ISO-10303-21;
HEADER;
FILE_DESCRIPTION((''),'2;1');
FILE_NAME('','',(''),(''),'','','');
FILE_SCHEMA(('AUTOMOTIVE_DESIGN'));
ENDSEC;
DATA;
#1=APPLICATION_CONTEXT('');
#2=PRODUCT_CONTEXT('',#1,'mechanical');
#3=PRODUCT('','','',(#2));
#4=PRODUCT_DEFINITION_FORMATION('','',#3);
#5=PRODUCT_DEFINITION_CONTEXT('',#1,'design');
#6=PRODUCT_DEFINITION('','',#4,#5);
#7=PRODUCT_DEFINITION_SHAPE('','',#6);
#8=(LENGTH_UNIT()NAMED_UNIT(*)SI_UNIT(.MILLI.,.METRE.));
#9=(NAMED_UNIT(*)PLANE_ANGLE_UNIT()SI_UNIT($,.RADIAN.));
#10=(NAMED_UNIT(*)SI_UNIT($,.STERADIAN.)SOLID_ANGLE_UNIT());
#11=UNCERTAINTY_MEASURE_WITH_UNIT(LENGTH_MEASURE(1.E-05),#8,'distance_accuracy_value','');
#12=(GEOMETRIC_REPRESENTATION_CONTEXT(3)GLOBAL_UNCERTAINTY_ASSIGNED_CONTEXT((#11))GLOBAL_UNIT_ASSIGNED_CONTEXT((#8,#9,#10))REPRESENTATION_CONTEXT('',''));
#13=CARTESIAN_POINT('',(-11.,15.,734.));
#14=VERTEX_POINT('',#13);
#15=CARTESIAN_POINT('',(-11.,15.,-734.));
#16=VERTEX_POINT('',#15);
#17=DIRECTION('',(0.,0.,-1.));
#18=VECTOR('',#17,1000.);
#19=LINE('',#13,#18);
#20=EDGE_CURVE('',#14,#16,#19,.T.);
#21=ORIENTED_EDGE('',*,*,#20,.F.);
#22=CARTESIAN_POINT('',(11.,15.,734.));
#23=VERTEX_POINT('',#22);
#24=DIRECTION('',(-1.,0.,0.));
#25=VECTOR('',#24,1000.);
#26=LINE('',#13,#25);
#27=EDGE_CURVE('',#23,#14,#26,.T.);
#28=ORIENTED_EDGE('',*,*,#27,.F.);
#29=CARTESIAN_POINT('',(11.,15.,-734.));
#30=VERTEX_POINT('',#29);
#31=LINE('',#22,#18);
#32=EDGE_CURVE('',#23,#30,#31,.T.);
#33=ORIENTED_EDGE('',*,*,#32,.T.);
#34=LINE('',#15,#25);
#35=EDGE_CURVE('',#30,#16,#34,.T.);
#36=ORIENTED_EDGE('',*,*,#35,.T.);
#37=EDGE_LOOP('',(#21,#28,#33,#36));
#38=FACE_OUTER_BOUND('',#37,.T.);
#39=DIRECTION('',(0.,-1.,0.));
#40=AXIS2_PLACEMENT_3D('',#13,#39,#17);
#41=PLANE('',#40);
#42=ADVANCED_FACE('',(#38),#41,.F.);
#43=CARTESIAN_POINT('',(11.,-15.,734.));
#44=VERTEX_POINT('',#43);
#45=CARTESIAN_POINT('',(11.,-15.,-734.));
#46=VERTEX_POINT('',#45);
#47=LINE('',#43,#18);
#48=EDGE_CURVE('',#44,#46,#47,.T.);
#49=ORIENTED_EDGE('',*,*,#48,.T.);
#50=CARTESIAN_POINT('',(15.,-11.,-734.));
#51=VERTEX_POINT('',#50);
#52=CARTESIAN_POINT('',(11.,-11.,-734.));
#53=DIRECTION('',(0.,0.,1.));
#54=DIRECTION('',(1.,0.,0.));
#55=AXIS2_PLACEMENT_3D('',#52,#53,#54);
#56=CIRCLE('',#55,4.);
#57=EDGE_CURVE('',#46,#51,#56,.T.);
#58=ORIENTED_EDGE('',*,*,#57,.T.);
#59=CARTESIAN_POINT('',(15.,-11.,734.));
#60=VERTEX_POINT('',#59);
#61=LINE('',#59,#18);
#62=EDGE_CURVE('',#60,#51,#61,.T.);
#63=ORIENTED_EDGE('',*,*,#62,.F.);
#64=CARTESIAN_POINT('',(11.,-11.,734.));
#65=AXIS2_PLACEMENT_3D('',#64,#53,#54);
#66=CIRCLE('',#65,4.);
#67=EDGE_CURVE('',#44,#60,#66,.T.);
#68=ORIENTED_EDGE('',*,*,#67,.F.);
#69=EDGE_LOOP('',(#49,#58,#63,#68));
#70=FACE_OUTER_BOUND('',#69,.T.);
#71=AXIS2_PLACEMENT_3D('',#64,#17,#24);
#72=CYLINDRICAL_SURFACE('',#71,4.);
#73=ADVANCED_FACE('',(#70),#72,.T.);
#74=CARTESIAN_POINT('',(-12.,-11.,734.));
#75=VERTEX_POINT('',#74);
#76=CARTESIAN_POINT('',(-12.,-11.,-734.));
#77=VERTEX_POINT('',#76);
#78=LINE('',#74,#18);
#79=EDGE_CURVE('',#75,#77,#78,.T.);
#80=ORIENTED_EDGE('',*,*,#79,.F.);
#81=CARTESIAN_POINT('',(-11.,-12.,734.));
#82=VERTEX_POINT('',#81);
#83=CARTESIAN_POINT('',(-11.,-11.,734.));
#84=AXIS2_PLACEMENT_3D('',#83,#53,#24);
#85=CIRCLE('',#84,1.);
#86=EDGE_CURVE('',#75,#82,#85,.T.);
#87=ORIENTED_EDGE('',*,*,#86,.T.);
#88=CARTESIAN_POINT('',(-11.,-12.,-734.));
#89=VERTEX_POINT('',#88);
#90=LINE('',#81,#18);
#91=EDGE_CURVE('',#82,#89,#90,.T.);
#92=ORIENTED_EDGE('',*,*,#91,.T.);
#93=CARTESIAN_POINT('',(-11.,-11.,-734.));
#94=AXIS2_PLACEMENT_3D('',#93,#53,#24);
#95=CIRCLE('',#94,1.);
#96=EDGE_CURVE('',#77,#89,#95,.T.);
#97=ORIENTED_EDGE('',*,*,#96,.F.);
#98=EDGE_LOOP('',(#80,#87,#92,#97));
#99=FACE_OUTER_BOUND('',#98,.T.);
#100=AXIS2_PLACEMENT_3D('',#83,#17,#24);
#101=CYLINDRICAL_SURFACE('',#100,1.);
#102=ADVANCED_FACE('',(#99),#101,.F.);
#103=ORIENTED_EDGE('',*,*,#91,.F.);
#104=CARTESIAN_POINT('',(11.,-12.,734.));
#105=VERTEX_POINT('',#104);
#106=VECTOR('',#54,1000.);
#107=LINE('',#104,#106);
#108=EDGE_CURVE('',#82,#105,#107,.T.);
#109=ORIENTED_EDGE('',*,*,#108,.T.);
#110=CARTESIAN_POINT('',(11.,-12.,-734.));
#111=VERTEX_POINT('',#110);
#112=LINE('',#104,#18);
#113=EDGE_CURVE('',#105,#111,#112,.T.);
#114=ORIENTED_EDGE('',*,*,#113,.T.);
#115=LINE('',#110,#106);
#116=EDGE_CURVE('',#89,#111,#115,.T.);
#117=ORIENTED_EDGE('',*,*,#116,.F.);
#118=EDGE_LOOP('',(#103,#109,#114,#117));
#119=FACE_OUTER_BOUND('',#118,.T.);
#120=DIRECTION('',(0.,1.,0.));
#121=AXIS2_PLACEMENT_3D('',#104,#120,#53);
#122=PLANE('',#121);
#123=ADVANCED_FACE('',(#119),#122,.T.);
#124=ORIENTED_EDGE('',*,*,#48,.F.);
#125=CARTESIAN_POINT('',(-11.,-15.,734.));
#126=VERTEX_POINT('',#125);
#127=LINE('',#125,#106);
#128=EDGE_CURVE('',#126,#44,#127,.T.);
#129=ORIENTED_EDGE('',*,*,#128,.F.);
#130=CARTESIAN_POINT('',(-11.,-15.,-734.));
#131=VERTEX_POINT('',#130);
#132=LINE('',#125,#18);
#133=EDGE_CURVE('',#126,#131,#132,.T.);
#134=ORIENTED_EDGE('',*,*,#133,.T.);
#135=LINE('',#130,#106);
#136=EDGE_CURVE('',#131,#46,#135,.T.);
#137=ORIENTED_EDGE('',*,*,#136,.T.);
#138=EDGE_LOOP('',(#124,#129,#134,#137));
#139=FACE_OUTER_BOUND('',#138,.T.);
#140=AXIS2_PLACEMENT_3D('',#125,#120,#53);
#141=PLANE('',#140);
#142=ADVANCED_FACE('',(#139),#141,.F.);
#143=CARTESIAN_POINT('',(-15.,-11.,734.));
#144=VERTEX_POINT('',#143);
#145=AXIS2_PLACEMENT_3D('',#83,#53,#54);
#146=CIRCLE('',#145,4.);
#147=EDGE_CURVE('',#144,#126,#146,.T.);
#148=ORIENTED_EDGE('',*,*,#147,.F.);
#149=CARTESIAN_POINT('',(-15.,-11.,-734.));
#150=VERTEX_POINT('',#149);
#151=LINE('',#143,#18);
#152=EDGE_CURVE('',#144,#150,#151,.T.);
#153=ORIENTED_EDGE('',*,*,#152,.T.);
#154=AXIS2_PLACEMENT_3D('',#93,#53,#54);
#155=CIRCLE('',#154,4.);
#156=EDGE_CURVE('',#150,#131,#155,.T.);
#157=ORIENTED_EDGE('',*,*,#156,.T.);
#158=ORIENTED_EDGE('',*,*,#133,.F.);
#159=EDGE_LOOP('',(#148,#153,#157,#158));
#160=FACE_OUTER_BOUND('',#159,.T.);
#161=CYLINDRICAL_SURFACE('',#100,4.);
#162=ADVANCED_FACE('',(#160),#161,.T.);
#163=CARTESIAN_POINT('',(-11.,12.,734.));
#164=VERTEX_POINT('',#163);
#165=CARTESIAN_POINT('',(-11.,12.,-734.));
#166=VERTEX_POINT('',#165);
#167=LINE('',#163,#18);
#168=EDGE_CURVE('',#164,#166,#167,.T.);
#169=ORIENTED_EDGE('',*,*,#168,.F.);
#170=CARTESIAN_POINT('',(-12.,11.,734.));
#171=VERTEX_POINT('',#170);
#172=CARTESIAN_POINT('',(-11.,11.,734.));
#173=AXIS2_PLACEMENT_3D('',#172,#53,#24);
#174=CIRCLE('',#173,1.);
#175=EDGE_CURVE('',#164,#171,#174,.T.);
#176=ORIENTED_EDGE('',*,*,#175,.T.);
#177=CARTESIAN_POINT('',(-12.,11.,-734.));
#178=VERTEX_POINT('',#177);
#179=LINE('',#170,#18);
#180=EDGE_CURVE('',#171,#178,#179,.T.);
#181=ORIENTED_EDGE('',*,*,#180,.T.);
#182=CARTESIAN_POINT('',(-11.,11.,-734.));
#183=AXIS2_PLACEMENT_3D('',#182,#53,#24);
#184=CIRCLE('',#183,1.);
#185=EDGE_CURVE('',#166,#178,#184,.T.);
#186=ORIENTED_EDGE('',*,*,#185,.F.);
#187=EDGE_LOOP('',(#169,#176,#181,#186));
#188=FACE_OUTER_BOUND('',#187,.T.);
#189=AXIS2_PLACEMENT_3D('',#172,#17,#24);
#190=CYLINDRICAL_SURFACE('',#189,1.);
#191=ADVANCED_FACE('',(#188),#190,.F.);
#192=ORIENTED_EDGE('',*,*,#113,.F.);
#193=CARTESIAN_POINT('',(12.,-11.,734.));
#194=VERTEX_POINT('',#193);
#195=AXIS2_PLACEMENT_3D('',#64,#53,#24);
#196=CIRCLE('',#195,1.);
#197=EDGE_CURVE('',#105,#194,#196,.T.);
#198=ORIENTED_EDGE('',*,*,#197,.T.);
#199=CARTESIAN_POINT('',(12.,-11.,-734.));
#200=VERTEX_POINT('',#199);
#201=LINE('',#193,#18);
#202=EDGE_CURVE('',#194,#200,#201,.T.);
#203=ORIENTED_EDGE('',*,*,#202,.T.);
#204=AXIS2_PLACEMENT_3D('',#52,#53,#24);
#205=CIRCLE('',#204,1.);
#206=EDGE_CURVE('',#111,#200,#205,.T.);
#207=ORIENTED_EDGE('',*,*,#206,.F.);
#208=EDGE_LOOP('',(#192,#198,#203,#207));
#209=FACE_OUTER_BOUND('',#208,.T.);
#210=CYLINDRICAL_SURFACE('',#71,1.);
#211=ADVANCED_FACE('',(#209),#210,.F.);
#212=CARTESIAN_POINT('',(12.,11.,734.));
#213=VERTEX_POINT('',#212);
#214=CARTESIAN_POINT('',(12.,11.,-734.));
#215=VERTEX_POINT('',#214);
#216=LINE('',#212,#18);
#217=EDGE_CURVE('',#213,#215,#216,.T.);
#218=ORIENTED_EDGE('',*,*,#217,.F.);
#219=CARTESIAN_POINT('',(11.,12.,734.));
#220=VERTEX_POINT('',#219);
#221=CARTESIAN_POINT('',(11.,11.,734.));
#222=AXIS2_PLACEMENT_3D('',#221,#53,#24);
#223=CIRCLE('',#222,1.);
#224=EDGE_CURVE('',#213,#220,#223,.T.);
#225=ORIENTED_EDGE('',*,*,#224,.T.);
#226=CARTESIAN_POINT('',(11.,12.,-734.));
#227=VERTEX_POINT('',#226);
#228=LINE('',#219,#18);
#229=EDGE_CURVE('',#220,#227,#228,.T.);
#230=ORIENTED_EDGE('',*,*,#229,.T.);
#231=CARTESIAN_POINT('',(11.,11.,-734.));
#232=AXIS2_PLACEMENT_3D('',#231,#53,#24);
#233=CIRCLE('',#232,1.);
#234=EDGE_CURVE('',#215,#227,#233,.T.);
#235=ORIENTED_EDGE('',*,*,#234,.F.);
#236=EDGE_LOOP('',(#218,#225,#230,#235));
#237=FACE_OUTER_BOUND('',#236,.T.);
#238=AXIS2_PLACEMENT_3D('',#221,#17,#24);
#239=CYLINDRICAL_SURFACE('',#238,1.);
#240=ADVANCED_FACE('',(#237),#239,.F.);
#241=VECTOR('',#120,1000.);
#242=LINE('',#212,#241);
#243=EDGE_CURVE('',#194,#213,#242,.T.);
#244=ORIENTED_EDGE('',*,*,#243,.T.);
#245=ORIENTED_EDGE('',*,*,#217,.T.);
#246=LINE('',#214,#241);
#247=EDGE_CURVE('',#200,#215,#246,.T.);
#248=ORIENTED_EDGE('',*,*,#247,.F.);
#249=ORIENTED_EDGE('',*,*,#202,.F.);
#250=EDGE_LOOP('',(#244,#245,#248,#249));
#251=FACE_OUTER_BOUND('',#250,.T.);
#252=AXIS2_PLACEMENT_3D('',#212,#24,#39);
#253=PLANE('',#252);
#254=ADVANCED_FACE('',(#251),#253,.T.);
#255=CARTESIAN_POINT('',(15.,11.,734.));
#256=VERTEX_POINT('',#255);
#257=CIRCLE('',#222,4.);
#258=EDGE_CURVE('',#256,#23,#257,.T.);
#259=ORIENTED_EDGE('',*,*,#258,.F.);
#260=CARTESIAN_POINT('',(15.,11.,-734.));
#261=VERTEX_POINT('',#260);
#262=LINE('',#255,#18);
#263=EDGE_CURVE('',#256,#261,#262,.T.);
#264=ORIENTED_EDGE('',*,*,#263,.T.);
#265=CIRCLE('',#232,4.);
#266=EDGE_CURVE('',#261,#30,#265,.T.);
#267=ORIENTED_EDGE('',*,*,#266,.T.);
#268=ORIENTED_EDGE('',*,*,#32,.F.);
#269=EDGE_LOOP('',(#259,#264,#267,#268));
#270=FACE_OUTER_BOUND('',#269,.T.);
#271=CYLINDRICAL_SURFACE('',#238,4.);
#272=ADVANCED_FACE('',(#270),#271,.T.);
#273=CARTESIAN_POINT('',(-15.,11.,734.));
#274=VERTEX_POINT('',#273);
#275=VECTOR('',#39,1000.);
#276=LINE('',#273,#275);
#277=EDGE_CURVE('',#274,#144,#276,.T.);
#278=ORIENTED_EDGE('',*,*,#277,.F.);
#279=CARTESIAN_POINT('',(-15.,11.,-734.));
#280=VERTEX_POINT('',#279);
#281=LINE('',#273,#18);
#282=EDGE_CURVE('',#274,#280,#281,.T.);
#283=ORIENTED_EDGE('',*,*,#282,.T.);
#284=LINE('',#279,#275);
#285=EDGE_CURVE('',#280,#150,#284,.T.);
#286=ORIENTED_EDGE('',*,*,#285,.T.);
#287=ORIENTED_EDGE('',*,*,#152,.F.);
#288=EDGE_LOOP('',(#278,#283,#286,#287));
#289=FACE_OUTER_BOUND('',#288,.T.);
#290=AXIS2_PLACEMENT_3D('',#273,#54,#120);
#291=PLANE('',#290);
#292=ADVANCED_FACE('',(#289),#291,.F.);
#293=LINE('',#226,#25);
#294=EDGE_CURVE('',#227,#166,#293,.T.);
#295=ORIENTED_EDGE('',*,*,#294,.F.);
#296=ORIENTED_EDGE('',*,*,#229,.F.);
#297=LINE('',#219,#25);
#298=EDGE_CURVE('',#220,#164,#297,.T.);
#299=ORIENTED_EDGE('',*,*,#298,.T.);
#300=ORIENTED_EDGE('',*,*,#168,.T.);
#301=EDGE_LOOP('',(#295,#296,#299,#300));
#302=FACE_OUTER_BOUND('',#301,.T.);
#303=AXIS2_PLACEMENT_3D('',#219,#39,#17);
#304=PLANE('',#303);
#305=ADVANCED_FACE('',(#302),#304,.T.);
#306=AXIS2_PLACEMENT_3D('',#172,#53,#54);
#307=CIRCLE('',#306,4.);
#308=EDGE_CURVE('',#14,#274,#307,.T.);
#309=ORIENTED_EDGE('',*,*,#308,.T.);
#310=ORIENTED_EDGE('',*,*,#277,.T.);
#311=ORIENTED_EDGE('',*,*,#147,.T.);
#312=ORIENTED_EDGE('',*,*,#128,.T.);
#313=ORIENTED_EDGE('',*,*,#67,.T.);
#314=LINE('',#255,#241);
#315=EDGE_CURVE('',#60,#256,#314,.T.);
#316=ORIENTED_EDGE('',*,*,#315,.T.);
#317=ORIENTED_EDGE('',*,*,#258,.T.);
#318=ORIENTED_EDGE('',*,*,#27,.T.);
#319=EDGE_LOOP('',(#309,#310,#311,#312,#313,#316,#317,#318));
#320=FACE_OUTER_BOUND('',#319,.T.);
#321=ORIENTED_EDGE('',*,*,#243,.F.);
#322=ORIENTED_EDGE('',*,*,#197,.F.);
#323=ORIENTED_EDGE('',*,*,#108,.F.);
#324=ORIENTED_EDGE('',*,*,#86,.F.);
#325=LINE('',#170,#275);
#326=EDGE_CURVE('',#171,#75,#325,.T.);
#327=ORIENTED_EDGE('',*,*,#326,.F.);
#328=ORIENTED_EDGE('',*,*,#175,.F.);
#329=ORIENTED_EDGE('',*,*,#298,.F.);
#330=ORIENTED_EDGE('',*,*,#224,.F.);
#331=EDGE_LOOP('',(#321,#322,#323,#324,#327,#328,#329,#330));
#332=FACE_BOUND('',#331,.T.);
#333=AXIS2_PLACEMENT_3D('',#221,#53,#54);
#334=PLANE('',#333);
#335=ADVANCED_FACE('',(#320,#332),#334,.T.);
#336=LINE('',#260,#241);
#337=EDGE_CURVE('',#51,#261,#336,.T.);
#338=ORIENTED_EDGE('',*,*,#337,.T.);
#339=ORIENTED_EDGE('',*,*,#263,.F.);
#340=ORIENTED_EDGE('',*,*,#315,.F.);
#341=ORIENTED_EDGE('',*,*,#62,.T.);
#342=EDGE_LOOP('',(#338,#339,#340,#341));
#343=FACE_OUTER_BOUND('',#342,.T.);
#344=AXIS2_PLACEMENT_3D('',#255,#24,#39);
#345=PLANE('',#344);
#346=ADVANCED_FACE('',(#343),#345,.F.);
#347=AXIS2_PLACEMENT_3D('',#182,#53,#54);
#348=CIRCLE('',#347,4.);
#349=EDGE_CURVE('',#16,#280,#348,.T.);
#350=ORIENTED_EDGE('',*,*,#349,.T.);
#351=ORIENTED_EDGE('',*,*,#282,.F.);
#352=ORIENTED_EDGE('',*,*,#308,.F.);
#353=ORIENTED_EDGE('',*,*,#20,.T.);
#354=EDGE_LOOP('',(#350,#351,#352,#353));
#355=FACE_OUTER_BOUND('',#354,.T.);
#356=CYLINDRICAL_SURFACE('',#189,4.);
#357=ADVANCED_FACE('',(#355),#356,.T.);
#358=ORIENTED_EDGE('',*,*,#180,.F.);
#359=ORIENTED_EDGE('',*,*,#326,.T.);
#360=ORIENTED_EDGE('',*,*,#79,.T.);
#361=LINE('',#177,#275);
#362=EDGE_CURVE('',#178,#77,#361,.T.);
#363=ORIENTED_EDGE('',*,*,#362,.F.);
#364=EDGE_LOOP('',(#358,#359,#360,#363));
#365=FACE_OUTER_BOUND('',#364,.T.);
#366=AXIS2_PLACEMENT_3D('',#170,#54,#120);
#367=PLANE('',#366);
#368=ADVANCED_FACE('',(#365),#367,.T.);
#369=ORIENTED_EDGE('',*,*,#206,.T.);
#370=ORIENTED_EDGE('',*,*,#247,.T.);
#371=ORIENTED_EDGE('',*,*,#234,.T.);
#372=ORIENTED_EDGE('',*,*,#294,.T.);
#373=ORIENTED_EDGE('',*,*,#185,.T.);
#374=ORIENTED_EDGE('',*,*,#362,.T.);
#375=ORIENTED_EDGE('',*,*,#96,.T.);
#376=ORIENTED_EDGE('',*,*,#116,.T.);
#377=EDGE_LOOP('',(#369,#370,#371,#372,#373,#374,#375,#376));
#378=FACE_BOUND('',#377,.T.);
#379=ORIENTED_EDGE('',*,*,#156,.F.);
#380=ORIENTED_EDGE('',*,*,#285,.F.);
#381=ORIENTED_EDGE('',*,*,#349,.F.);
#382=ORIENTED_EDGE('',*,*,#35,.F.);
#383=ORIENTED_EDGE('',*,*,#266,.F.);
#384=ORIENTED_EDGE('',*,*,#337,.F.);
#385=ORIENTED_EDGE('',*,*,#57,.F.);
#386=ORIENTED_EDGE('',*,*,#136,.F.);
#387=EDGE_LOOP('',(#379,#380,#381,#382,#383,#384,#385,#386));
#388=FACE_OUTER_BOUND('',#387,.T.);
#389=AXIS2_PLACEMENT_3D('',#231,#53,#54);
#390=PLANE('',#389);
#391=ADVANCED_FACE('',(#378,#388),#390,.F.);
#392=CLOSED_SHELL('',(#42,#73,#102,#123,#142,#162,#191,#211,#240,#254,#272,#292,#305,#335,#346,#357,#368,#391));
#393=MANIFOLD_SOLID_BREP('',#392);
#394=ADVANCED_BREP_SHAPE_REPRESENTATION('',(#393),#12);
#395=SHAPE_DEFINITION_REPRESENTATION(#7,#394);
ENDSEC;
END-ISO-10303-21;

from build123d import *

# Parameters (mm, degrees)
EXTRUDE_1_DEPTH = 734


with BuildPart() as part:
    # 草图2 → 拉伸-薄壁1 (new, symmetric)
    with BuildSketch(Plane.XY):
        with BuildLine():
            Line((-11, 15), (11, 15))
            ThreePointArc((11, 15), (13.828427125, 13.828427125), (15, 11))
            Line((15, 11), (15, -11))
            ThreePointArc((15, -11), (13.828427125, -13.828427125), (11, -15))
            Line((11, -15), (-11, -15))
            ThreePointArc((-11, -15), (-13.828427125, -13.828427125), (-15, -11))
            Line((-15, -11), (-15, 11))
            ThreePointArc((-15, 11), (-13.828427125, 13.828427125), (-11, 15))
        make_face()
        with BuildLine():
            Line((-11, 12), (11, 12))
            ThreePointArc((11, 12), (11.707106781, 11.707106781), (12, 11))
            Line((12, 11), (12, -11))
            ThreePointArc((12, -11), (11.707106781, -11.707106781), (11, -12))
            Line((11, -12), (-11, -12))
            ThreePointArc((-11, -12), (-11.707106781, -11.707106781), (-12, -11))
            Line((-12, -11), (-12, 11))
            ThreePointArc((-12, 11), (-11.707106781, 11.707106781), (-11, 12))
        make_face(mode=Mode.SUBTRACT)
    extrude(amount=EXTRUDE_1_DEPTH, both=True)


solid = part.part
